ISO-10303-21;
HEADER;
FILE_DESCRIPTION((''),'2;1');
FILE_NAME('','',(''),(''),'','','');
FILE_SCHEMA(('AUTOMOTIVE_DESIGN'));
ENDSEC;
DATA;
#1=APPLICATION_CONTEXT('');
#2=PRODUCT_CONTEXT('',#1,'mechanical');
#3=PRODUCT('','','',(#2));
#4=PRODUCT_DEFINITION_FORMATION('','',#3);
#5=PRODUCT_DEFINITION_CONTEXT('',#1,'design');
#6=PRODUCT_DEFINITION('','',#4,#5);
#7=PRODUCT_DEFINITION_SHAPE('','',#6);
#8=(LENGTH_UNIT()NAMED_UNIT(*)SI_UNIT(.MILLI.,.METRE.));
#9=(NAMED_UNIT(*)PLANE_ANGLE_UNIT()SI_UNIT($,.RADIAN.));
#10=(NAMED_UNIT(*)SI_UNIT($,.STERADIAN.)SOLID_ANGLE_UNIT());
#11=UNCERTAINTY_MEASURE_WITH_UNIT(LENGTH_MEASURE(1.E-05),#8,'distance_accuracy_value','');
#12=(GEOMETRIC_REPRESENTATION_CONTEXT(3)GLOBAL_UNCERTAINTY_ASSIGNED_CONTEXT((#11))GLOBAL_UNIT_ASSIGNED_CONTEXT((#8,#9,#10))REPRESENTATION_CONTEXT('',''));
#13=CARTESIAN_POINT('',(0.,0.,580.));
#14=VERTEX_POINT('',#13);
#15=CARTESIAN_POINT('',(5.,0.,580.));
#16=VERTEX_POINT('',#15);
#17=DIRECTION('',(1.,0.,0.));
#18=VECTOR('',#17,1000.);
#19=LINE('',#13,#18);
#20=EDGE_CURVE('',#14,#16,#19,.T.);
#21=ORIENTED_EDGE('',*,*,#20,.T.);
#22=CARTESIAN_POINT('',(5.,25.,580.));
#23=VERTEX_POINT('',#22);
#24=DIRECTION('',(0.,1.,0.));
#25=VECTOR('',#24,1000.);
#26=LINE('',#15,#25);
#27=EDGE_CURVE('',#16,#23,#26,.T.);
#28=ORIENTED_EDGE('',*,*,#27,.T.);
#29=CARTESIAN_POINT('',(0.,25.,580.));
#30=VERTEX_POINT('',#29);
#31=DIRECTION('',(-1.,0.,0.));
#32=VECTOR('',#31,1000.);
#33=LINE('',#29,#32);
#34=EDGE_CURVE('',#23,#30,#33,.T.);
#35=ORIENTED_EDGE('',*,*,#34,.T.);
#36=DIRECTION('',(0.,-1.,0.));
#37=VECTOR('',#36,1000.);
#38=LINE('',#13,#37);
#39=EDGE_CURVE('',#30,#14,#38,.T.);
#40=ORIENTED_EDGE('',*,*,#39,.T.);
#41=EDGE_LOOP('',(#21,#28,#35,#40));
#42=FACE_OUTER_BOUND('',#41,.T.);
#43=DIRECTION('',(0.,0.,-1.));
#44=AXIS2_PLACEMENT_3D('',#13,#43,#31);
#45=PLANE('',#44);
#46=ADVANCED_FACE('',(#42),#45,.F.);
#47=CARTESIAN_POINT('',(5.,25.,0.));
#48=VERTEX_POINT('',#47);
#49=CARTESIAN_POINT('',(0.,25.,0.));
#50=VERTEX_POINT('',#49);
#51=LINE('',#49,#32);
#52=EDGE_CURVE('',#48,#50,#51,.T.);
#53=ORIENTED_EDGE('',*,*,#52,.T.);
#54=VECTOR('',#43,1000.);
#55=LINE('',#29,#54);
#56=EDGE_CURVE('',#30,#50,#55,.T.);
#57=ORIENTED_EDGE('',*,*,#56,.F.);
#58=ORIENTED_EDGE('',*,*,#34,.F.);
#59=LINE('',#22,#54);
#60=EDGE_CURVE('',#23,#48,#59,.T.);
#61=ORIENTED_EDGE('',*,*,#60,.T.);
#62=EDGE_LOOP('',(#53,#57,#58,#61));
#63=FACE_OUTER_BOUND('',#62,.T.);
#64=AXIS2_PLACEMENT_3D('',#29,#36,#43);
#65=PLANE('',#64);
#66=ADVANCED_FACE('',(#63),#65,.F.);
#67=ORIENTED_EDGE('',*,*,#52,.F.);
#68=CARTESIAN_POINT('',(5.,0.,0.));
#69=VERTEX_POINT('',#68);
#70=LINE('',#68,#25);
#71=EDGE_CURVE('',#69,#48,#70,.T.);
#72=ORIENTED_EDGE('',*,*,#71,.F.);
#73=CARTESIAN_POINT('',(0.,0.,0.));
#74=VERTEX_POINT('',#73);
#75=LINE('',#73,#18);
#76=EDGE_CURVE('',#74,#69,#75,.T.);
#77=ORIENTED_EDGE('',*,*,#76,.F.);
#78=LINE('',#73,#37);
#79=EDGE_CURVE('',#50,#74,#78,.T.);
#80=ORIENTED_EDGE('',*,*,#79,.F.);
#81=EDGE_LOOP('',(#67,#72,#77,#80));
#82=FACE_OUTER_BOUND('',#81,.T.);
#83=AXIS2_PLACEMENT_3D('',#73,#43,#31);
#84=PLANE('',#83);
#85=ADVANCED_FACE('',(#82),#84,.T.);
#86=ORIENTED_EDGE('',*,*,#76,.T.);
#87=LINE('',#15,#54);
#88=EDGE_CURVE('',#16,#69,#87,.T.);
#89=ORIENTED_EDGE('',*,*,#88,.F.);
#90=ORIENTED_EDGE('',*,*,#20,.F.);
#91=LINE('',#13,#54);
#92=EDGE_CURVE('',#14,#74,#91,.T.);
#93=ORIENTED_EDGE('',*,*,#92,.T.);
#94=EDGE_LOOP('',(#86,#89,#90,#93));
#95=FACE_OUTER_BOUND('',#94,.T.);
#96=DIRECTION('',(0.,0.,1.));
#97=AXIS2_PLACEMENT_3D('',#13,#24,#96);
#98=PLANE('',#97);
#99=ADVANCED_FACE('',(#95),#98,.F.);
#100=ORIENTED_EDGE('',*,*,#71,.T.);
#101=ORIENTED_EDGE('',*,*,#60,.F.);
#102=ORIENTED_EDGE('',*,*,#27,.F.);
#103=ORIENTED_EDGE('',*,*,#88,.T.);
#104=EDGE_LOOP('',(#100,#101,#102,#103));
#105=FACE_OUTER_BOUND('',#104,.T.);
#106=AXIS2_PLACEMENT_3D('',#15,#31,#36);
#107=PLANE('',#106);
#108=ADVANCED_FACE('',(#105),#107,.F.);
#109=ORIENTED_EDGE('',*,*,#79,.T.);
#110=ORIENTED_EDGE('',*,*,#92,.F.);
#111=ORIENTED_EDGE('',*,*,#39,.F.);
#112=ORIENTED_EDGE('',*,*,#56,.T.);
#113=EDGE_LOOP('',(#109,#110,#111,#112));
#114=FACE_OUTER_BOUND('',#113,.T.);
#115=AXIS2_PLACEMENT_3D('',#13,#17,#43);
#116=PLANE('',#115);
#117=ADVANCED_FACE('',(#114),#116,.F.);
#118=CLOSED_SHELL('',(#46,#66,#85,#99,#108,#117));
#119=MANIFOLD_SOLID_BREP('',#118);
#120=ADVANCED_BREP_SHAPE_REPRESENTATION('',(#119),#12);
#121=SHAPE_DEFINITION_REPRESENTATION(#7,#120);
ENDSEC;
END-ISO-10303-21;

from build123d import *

# Parameters (mm, degrees)
SKETCH1_W           = 5
SKETCH1_H           = 25
BOSS_EXTRUDE1_DEPTH = 580


with BuildPart() as part:
    # Sketch1 → Boss-Extrude1 (new body)
    with BuildSketch(Plane.XY):
        with Locations((2.5, 12.5)):
            Rectangle(SKETCH1_W, SKETCH1_H)
    extrude(amount=BOSS_EXTRUDE1_DEPTH)


solid = part.part
